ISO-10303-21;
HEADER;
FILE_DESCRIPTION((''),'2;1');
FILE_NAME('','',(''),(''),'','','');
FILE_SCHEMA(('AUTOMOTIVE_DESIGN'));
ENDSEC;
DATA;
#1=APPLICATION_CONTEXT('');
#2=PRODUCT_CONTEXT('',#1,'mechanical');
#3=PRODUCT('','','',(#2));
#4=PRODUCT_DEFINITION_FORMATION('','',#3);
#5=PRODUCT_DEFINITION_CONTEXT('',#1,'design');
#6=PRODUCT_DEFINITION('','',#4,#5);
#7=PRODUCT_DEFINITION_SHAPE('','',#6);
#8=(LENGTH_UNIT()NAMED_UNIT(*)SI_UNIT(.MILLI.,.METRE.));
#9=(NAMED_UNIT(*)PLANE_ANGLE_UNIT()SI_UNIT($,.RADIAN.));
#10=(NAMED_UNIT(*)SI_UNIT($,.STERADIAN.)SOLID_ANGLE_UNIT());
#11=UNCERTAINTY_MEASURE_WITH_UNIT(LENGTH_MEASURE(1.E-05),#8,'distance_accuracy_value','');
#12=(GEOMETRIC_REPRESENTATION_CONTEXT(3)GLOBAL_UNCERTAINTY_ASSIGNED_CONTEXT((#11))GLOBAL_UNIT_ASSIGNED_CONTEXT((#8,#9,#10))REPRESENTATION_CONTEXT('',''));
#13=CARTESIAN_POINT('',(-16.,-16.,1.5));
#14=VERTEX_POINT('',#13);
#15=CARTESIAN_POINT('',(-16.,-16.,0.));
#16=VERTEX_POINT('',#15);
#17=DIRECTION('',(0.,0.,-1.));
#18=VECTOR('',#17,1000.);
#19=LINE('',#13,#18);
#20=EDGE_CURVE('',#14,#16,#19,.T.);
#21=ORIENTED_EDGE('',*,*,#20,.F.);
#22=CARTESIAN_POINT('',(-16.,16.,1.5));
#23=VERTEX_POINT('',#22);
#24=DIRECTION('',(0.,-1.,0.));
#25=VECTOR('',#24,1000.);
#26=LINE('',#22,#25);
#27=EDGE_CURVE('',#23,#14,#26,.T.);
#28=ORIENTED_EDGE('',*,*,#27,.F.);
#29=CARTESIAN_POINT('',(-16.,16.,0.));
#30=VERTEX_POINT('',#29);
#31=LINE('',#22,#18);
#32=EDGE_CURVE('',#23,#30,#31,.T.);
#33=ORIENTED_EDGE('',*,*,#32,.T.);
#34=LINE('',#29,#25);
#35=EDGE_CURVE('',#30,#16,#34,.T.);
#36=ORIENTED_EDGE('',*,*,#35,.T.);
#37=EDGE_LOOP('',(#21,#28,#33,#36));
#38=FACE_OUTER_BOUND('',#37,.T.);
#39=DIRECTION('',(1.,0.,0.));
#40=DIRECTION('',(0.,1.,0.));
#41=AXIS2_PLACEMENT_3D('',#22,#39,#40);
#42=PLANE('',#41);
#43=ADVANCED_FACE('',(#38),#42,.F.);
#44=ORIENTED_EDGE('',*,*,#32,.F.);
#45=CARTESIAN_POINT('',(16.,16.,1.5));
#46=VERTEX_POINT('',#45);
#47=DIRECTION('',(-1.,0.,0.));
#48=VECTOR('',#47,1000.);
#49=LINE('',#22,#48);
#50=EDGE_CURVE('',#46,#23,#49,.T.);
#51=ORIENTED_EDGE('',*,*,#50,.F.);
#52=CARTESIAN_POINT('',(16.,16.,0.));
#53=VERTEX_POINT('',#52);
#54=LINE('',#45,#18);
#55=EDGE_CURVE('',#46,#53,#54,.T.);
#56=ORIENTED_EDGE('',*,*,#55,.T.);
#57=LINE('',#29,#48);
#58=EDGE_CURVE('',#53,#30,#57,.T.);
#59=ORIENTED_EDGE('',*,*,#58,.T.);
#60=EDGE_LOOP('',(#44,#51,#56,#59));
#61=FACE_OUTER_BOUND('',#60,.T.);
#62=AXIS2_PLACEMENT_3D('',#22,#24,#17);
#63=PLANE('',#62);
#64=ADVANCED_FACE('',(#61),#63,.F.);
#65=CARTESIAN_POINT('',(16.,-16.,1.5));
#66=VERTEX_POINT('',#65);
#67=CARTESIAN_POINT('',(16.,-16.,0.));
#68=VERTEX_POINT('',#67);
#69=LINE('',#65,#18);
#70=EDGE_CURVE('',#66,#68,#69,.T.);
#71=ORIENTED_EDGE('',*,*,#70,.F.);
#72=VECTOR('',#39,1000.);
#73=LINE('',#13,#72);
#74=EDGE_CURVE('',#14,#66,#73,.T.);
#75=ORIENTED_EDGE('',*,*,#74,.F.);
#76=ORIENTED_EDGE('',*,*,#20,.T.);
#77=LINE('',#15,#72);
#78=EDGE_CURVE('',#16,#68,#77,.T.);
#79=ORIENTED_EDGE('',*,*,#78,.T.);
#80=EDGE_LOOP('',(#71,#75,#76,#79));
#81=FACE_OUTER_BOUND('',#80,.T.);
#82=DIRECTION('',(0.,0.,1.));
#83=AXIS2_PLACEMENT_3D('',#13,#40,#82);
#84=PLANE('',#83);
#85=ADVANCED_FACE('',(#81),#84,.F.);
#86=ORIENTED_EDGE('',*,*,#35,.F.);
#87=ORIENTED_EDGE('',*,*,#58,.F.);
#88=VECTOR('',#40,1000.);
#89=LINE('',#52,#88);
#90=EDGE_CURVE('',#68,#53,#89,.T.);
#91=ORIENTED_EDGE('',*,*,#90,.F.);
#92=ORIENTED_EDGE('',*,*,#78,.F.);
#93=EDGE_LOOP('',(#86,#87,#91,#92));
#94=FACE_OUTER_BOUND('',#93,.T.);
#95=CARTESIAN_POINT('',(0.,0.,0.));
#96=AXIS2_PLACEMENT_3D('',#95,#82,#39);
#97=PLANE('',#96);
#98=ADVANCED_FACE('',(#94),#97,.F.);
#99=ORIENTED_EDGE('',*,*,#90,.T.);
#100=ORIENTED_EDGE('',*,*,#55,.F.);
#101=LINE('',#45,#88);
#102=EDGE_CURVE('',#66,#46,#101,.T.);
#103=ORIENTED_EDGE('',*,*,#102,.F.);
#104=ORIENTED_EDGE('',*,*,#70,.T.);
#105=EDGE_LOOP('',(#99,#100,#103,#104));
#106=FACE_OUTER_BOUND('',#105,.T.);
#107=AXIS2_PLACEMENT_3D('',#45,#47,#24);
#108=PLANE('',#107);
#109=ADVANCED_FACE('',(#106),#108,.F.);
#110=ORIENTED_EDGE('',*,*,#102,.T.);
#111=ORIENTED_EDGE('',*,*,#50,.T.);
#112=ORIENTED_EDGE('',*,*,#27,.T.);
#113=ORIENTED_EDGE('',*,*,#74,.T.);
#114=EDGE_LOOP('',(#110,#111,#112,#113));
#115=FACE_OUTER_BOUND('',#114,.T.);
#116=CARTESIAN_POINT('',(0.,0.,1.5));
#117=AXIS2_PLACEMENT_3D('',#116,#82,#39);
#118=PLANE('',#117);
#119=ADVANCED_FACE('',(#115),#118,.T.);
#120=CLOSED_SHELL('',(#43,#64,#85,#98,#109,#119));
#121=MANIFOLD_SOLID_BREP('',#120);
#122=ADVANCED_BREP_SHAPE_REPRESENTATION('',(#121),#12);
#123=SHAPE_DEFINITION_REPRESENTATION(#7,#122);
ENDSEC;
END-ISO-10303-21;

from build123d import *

# Parameters (mm, degrees)
SKETCH1_W           = 32
SKETCH1_H           = 32
BOSS_EXTRUDE1_DEPTH = 1.5


with BuildPart() as part:
    # Sketch1 → Boss-Extrude1 (new body)
    with BuildSketch(Plane.XY):
        Rectangle(SKETCH1_W, SKETCH1_H)
    extrude(amount=BOSS_EXTRUDE1_DEPTH)


solid = part.part
